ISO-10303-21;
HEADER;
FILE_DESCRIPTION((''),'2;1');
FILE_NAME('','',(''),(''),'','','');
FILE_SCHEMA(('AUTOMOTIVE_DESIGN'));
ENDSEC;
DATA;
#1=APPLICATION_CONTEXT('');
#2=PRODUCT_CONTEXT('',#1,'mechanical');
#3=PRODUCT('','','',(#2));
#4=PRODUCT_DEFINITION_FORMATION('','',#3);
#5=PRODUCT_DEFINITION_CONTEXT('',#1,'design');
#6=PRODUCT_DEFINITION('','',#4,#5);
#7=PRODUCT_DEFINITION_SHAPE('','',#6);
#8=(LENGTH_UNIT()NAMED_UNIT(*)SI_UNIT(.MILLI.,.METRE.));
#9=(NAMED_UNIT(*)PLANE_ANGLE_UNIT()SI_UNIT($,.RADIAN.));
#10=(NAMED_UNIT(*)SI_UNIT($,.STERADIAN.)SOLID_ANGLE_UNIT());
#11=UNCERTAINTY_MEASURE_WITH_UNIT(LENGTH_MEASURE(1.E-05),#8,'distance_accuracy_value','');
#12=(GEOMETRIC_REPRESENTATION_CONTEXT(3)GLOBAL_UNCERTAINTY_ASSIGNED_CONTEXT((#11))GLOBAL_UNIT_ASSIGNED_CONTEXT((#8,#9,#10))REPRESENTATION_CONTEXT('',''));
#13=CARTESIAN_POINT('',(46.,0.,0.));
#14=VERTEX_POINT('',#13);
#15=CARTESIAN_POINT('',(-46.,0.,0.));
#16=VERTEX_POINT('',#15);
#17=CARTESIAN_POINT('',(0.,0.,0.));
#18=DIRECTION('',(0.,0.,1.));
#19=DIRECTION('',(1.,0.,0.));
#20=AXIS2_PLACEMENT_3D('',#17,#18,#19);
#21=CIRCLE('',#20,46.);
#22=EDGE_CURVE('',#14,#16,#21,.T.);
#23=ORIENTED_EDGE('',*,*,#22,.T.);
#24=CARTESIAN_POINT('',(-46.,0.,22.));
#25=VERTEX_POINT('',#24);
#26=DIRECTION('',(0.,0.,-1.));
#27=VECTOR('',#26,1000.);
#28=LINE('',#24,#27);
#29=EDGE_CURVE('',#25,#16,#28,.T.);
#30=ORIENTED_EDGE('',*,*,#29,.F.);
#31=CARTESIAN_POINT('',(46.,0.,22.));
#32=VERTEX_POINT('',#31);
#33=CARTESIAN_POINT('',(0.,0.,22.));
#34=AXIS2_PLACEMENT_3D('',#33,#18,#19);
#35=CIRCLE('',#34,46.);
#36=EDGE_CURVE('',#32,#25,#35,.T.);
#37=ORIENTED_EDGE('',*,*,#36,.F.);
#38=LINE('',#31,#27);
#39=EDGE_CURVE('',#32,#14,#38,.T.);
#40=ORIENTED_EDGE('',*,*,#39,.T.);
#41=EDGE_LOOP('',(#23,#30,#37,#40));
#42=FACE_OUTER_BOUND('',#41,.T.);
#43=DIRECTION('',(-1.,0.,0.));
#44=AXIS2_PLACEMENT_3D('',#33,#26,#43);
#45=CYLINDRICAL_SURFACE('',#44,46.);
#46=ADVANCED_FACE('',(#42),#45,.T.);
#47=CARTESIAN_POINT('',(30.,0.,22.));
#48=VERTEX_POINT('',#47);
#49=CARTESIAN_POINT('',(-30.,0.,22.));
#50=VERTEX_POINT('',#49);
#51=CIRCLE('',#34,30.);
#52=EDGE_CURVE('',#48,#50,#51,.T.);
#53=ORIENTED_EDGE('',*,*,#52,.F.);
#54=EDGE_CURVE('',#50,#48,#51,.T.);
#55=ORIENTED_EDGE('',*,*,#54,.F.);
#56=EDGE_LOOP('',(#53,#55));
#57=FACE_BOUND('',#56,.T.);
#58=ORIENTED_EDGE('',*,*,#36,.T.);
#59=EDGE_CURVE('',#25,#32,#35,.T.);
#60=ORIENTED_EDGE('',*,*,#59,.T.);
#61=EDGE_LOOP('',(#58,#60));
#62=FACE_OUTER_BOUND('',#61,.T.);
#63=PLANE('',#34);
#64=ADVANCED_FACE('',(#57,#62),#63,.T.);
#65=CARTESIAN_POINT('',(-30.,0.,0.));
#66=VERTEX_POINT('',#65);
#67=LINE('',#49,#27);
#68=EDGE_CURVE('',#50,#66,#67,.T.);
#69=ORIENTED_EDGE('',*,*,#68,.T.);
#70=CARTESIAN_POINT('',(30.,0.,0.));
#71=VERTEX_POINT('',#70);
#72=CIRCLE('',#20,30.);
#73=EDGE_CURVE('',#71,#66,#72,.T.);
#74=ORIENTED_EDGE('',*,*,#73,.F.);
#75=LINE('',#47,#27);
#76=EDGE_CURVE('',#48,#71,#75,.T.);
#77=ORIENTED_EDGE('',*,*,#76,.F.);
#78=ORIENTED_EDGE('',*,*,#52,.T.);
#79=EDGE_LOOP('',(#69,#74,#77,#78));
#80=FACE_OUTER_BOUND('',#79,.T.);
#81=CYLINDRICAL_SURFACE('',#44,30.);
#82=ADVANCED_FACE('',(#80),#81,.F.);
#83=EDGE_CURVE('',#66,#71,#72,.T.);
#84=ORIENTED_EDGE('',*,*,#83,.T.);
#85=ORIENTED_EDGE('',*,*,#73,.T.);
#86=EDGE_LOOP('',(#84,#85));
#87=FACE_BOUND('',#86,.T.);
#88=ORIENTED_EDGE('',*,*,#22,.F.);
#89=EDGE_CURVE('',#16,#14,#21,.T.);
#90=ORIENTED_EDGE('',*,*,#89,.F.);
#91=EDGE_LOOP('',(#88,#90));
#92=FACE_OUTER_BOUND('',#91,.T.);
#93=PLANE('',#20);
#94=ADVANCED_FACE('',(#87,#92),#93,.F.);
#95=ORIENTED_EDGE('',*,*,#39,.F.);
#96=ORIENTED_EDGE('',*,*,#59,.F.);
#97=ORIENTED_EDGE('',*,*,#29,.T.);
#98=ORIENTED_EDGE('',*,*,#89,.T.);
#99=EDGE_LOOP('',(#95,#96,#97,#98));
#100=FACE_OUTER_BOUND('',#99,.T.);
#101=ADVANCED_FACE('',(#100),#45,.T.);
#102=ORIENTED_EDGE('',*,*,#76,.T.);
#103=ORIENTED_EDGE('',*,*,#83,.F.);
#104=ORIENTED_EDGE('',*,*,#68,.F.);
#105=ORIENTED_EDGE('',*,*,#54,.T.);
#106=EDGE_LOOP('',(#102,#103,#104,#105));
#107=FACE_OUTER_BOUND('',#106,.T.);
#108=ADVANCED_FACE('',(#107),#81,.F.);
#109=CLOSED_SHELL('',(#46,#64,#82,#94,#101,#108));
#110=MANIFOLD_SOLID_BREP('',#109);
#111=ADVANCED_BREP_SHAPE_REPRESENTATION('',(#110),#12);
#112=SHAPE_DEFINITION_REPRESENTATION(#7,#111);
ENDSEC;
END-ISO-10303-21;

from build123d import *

# Parameters (mm, degrees)
SKETCH1_R           = 46
SKETCH1_R_2         = 30
BOSS_EXTRUDE1_DEPTH = 22


with BuildPart() as part:
    # Sketch1 → Boss-Extrude1 (new body)
    with BuildSketch(Plane.XY):
        Circle(SKETCH1_R)
        Circle(SKETCH1_R_2, mode=Mode.SUBTRACT)
    extrude(amount=BOSS_EXTRUDE1_DEPTH)


solid = part.part
